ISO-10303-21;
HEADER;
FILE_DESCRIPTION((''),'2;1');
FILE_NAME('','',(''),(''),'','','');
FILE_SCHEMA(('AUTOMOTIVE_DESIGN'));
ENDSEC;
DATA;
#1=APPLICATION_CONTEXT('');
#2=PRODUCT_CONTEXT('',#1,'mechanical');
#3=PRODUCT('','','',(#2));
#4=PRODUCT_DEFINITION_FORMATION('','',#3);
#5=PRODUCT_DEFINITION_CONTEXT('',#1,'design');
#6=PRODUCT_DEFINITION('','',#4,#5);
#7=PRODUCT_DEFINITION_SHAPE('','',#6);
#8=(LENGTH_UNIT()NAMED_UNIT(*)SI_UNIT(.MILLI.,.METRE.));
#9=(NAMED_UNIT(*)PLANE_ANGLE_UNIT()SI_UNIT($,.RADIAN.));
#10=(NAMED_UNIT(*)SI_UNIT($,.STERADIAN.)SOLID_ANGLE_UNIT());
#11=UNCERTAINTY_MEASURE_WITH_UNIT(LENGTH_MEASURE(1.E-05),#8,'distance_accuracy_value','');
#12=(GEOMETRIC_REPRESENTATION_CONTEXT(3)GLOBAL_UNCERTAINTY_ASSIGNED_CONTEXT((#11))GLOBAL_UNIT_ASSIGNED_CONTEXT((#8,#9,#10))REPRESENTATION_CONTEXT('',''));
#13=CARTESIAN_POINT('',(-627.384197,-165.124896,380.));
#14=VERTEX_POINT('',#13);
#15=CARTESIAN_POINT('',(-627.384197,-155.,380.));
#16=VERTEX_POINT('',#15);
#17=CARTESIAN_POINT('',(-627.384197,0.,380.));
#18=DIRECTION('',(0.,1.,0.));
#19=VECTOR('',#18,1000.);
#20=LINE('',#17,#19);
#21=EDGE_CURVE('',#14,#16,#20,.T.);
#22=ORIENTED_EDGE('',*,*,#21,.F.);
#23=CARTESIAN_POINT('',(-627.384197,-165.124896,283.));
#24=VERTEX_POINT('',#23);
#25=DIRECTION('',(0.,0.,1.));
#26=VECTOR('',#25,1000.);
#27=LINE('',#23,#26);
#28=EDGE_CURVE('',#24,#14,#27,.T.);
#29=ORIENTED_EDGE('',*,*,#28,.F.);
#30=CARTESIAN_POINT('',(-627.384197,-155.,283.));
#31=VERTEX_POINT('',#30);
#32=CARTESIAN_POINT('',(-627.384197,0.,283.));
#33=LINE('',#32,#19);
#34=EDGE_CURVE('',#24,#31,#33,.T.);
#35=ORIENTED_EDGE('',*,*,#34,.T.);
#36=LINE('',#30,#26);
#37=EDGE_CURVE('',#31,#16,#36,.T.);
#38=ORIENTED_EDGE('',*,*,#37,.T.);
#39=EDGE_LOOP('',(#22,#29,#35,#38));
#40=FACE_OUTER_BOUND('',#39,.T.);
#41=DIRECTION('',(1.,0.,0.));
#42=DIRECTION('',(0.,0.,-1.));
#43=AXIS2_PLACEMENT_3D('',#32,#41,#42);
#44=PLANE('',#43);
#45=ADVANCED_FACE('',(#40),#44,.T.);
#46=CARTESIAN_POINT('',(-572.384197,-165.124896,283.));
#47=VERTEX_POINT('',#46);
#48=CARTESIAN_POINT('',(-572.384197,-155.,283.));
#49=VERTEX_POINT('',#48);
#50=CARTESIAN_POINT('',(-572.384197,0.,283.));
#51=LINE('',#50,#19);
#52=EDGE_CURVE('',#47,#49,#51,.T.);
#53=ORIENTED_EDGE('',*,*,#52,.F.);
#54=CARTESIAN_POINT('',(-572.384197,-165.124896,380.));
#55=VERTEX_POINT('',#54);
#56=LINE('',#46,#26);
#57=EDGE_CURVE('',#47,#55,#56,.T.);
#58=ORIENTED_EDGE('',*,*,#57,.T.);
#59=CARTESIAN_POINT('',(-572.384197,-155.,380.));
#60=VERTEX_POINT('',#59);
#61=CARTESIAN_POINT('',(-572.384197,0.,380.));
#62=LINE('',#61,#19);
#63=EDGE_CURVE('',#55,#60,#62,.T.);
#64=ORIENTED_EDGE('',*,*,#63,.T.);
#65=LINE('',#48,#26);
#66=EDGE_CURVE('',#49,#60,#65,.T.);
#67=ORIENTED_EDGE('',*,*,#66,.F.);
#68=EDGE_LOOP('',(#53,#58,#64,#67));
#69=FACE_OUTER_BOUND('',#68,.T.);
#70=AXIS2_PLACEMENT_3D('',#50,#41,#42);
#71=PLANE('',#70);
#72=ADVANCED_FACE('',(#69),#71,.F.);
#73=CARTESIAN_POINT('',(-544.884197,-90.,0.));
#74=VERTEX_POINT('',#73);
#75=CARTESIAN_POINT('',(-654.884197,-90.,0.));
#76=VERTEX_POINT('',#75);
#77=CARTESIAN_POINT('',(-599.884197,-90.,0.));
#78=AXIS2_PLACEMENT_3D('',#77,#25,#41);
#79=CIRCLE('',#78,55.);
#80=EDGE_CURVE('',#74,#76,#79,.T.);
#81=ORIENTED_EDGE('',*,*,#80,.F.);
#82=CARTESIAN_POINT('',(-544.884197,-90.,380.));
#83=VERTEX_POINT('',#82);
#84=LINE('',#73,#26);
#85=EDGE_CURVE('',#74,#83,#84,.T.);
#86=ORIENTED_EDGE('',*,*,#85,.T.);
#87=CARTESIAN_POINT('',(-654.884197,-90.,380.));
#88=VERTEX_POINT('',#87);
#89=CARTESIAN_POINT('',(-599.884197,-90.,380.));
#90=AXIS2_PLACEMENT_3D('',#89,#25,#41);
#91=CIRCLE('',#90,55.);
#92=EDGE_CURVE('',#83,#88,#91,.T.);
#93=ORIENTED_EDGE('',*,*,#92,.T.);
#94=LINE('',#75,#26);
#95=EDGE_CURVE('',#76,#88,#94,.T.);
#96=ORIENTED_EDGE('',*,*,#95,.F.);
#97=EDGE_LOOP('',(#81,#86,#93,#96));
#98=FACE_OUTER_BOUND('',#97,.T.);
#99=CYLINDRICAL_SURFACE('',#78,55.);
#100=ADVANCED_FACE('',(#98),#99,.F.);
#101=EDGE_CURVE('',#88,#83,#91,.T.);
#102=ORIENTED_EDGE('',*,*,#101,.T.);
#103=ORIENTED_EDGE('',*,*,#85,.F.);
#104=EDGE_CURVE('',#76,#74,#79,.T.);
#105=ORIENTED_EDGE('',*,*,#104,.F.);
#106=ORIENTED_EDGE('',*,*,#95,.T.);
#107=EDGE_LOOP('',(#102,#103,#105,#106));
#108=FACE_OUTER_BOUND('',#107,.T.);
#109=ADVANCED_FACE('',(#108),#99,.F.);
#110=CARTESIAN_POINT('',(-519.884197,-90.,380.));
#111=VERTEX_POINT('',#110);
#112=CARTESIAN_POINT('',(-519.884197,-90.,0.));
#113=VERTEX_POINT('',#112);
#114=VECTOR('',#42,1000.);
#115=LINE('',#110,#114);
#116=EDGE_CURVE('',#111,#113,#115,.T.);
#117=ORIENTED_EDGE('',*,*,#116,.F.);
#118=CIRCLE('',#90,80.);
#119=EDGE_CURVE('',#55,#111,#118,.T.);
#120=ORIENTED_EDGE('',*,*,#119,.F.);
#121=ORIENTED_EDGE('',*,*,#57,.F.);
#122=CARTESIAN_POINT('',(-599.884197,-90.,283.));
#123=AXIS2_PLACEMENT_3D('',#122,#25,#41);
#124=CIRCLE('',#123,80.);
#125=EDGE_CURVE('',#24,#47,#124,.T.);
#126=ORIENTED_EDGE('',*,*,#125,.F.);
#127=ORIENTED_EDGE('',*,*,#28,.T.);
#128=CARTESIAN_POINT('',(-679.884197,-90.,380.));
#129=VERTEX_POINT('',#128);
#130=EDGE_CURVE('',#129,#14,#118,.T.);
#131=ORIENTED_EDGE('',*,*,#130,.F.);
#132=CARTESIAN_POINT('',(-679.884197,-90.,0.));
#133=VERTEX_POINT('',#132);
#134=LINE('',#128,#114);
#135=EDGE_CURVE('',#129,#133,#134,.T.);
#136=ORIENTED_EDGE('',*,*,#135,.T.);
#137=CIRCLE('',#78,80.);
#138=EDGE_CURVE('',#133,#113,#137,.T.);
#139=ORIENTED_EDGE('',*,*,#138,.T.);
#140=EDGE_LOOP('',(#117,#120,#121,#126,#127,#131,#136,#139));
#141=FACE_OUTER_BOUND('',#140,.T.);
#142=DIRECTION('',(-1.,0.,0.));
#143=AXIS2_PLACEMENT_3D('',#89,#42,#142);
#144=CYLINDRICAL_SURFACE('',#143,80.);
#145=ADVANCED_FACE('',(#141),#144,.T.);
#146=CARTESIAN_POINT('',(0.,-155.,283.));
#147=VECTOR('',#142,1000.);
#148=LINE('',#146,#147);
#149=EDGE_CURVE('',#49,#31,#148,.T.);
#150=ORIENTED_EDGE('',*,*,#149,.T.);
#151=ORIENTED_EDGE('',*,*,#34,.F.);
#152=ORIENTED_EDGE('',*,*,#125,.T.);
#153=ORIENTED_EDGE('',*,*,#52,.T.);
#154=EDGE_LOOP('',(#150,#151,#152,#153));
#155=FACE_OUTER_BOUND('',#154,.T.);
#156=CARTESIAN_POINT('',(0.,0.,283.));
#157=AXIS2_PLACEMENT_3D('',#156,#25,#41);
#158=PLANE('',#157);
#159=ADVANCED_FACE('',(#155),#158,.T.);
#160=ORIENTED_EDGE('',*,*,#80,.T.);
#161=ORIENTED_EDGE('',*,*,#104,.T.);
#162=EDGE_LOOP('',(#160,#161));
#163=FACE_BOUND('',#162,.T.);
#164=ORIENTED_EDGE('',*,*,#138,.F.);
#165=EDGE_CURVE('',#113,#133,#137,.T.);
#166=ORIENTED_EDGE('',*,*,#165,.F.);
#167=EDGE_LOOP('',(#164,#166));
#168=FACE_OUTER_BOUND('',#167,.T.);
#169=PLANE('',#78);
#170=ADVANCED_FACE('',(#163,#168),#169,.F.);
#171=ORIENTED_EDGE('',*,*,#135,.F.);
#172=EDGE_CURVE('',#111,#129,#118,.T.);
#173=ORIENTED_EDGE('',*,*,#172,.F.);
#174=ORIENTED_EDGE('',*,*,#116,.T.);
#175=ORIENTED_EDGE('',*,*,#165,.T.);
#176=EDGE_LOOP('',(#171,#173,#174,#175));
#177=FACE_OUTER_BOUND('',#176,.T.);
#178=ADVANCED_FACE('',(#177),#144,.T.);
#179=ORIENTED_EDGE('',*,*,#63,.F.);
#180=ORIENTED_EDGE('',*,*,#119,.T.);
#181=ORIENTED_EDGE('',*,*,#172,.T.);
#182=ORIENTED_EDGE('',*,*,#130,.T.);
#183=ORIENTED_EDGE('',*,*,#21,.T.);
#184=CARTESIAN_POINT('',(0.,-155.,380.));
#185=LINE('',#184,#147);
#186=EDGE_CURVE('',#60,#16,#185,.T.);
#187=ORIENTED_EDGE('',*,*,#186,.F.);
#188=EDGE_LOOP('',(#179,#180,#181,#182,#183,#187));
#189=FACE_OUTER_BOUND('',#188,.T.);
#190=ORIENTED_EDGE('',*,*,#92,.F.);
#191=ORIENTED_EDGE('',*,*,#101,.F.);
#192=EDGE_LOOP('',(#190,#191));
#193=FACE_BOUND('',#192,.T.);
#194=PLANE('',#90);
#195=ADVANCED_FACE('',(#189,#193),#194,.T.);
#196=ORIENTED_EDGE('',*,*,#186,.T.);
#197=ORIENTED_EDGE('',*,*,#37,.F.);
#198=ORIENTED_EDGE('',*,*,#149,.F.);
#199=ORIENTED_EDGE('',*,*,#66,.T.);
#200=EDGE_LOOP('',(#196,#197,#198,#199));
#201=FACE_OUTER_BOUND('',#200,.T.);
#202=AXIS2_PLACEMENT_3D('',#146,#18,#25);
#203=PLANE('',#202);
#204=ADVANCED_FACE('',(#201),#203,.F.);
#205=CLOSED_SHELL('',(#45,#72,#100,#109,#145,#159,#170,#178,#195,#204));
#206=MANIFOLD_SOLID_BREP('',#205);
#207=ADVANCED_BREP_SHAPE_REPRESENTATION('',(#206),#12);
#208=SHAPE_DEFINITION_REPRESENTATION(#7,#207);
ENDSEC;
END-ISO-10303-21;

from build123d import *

# Parameters (mm, degrees)
SKETCH1_R               = 80
BOSS_EXTRUDE1_DEPTH     = 380
CUT_EXTRUDE1_START      = -97
CUT_EXTRUDE1_DEPTH      = 97
CUT_EXTRUDE2_DEPTH      = 798.2092078
CUT_EXTRUDE2_DEPTH_BACK = 798.2092078
SKETCH3_R               = 55


with BuildPart() as part:
    # Sketch1 → Boss-Extrude1 (new body)
    with BuildSketch(Plane.XY):
        with Locations((-599.884196758, -90)):
            Circle(SKETCH1_R)
    extrude(amount=BOSS_EXTRUDE1_DEPTH)

    # Sketch2 → Cut-Extrude1 (cut)
    with BuildSketch(Plane.XY.offset(380).offset(CUT_EXTRUDE1_START)):
        with BuildLine():
            ThreePointArc((-627.384196758, -165.124896007), (-599.884196758, -170), (-572.384196758, -165.124896007))
            Line((-572.384196758, -165.124896007), (-572.384196758, -155))
            Line((-572.384196758, -155), (-627.384196758, -155))
            Line((-627.384196758, -155), (-627.384196758, -165.124896007))
        make_face()
    extrude(amount=CUT_EXTRUDE1_DEPTH, mode=Mode.SUBTRACT)

    # Sketch3 → Cut-Extrude2 (cut, two sides: drawn at the far end of the back side and taken through both)
    with BuildSketch(Plane.XY.offset(380).offset(-CUT_EXTRUDE2_DEPTH_BACK)):
        with Locations((-599.884196758, -90)):
            Circle(SKETCH3_R)
    extrude(amount=CUT_EXTRUDE2_DEPTH + CUT_EXTRUDE2_DEPTH_BACK, mode=Mode.SUBTRACT)


solid = part.part
